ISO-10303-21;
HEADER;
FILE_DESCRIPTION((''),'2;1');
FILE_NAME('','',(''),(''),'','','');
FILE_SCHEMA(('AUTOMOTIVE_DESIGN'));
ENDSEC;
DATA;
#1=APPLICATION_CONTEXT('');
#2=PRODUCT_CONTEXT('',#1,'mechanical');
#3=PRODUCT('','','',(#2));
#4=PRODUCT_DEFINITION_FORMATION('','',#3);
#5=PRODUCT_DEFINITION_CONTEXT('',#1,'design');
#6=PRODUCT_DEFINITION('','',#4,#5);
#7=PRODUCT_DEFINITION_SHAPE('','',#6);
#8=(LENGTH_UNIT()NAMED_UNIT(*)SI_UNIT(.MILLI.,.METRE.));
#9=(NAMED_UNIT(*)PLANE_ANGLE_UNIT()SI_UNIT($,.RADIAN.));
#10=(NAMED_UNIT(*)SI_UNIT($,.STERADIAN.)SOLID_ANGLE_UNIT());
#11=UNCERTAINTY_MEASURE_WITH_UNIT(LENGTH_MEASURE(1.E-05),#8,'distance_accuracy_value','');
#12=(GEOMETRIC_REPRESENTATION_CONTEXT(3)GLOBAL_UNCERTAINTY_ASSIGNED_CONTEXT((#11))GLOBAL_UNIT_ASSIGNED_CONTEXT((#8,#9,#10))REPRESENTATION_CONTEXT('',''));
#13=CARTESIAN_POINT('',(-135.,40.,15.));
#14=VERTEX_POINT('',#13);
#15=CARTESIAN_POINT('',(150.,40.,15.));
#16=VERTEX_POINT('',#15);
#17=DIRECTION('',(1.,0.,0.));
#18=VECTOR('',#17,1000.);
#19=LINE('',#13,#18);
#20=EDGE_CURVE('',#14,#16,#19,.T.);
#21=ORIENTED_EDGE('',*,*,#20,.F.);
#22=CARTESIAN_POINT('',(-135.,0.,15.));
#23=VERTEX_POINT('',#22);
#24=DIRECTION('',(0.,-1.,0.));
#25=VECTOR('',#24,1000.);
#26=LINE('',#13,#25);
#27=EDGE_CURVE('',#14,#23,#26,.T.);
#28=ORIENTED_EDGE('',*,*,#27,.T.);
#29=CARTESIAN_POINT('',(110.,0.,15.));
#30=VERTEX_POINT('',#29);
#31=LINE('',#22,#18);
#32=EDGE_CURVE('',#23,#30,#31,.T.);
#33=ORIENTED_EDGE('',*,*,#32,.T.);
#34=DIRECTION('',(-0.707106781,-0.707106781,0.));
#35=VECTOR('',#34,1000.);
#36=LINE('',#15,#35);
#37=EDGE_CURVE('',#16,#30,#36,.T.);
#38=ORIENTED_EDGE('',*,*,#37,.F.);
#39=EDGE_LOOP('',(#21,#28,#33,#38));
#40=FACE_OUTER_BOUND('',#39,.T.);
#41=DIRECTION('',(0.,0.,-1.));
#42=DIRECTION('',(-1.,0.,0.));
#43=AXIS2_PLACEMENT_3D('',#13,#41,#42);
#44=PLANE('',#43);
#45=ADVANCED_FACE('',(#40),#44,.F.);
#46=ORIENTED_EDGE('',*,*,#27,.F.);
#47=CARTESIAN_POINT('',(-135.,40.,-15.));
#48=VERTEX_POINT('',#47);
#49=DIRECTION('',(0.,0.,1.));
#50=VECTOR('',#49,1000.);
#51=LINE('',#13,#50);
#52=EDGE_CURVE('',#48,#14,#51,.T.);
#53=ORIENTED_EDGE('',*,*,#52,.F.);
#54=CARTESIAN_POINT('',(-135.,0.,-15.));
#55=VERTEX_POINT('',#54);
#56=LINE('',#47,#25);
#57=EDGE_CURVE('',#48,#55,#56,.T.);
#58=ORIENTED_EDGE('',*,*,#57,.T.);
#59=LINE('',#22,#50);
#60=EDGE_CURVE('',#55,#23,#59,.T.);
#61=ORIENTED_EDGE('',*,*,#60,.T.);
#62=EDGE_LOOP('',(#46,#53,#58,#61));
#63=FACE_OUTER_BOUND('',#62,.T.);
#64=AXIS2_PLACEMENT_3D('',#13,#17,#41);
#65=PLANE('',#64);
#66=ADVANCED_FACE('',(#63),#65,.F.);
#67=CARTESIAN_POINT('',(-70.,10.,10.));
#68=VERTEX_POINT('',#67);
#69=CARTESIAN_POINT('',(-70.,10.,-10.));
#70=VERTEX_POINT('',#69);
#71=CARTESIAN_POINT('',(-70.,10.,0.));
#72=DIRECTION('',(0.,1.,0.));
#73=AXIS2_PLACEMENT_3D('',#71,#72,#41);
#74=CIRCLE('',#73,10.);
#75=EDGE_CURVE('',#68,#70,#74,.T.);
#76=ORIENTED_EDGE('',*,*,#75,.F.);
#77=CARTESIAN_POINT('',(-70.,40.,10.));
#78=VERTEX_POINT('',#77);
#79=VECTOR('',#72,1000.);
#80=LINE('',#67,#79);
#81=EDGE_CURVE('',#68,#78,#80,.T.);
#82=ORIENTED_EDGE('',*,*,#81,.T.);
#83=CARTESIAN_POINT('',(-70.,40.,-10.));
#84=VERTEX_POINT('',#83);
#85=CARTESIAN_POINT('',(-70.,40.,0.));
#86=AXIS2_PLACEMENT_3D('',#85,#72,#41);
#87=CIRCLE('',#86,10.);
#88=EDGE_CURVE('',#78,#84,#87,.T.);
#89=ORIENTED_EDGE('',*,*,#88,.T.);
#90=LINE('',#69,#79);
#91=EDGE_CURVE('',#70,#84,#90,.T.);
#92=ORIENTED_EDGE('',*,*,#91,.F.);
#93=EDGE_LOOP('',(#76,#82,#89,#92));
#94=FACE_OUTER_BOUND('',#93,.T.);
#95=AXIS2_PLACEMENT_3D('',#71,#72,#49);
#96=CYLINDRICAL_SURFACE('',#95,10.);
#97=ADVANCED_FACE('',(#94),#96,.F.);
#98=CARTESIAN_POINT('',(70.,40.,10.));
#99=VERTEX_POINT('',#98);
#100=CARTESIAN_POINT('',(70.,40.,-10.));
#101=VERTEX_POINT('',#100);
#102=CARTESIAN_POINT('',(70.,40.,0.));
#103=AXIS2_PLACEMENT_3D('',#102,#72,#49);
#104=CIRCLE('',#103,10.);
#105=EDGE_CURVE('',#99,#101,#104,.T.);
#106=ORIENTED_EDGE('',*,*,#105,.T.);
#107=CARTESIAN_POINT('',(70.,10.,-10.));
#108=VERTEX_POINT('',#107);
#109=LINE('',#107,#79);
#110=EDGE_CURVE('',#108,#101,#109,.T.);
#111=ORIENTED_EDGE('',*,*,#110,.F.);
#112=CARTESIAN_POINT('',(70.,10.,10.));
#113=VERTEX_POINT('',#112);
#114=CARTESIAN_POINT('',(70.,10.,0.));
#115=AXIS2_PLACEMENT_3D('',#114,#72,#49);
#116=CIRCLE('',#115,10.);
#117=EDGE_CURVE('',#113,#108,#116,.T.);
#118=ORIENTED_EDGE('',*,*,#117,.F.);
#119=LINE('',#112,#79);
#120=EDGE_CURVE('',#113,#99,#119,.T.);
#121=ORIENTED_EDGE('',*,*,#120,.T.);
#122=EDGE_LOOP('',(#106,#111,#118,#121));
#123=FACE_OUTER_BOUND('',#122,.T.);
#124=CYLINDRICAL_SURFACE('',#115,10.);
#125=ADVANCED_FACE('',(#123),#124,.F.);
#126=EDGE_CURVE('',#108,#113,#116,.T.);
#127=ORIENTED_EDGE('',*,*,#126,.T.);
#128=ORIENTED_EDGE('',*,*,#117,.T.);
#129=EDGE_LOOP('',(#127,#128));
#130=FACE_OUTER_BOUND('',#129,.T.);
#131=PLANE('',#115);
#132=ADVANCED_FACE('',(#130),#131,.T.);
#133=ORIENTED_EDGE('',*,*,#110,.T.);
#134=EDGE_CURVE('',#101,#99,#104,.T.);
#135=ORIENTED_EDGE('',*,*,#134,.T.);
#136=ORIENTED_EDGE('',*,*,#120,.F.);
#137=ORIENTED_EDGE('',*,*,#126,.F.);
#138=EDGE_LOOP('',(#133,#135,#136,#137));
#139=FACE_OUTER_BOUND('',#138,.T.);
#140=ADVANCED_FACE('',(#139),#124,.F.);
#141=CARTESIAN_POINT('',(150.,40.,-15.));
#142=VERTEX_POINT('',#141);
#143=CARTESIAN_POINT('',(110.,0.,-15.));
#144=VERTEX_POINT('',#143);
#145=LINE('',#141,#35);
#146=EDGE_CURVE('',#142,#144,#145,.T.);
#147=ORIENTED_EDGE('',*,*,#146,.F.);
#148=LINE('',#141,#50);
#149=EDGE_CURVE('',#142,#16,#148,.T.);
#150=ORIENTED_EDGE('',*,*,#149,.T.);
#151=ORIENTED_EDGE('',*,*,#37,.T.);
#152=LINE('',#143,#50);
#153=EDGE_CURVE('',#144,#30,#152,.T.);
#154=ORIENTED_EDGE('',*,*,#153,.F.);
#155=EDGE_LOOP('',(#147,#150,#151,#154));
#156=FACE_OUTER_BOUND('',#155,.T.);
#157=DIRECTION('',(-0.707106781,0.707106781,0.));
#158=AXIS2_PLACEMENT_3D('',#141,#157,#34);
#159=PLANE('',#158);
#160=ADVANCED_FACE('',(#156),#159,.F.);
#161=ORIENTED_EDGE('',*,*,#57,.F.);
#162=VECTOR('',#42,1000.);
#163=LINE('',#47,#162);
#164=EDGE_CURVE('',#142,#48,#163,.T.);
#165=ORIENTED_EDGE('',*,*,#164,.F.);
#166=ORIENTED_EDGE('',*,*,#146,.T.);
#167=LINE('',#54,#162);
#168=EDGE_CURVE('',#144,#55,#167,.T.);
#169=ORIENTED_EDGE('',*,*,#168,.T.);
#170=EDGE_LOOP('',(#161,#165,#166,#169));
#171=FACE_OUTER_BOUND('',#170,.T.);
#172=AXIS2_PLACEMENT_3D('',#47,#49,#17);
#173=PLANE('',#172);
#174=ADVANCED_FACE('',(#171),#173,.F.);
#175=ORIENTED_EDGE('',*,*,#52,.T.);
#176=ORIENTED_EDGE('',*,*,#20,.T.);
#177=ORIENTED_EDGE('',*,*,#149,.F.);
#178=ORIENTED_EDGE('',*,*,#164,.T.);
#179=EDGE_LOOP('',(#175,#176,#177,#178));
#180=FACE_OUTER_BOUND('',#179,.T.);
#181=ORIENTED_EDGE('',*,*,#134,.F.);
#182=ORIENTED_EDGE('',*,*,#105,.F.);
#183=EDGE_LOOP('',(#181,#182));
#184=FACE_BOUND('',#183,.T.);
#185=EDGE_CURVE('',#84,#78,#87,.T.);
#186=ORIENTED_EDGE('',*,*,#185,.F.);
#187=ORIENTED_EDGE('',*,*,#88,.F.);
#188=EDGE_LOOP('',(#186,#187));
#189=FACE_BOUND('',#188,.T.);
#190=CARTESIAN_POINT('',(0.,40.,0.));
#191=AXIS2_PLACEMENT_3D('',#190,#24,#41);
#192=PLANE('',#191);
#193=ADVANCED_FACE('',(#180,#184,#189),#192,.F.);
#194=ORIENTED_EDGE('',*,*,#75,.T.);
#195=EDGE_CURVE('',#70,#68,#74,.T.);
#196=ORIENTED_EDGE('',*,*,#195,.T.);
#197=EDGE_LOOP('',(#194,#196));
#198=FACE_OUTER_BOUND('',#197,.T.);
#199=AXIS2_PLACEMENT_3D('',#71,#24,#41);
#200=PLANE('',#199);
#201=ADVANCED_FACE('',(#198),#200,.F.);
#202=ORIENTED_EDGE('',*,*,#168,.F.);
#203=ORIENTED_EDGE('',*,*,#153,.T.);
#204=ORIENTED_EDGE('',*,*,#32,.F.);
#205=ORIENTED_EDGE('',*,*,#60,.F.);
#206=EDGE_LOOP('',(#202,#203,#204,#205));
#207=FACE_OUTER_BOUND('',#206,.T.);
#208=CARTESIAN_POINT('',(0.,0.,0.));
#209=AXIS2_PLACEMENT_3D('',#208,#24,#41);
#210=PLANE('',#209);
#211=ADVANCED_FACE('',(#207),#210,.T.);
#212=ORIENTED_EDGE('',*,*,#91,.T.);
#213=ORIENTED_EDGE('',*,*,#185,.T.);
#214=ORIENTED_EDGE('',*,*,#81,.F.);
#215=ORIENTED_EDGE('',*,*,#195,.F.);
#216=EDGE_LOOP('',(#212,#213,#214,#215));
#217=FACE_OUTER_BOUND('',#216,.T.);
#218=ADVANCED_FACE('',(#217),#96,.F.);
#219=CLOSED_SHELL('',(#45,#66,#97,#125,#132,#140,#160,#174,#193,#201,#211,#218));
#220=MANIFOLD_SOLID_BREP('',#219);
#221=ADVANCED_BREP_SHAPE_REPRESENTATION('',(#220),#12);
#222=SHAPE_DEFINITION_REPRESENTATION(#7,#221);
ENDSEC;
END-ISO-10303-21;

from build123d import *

# Parameters (mm, degrees)
SKETCH_1_W          = 270
SKETCH_1_H          = 30
EXTRUDE_1_DEPTH     = 40
SKETCH_2_R          = 10
CUT_EXTRUDE_2_DEPTH = 30
SKETCH_3_W          = 30
SKETCH_3_H          = 40
EXTRUDE_2_DEPTH     = 15
CUT_EXTRUDE_3_DEPTH = 159.113883008


with BuildPart() as part:
    # 草图1 → 凸台-拉伸1 (new body)
    with BuildSketch(Plane(origin=(0, 0, 0), x_dir=(1, 0, 0), z_dir=(0, 1, 0))):
        Rectangle(SKETCH_1_W, SKETCH_1_H)
    extrude(amount=EXTRUDE_1_DEPTH)

    # 草图2 → 切除-拉伸2 (cut)
    with BuildSketch(Plane(origin=(0, 40, 0), x_dir=(1, 0, 0), z_dir=(0, 1, 0))):
        with Locations(Location((70, 0, 0), (0, 0, 270))):
            Circle(SKETCH_2_R)
        with Locations(Location((-70, 0, 0), (0, 0, 90))):
            Circle(SKETCH_2_R)
    extrude(amount=-CUT_EXTRUDE_2_DEPTH, mode=Mode.SUBTRACT)

    # 草图3 → 凸台-拉伸2 (add)
    with BuildSketch(Plane(origin=(135, 0, 0), x_dir=(0, 0, -1), z_dir=(1, 0, 0))):
        with Locations((0, 20)):
            Rectangle(SKETCH_3_W, SKETCH_3_H)
    extrude(amount=EXTRUDE_2_DEPTH)

    # 草图4 → 切除-拉伸3 (cut, through all)
    with BuildSketch(Plane.XY.offset(15)):
        Polygon((150, 40), (110, 0), (150, 0), align=None)
    extrude(amount=-CUT_EXTRUDE_3_DEPTH, mode=Mode.SUBTRACT)


solid = part.part
